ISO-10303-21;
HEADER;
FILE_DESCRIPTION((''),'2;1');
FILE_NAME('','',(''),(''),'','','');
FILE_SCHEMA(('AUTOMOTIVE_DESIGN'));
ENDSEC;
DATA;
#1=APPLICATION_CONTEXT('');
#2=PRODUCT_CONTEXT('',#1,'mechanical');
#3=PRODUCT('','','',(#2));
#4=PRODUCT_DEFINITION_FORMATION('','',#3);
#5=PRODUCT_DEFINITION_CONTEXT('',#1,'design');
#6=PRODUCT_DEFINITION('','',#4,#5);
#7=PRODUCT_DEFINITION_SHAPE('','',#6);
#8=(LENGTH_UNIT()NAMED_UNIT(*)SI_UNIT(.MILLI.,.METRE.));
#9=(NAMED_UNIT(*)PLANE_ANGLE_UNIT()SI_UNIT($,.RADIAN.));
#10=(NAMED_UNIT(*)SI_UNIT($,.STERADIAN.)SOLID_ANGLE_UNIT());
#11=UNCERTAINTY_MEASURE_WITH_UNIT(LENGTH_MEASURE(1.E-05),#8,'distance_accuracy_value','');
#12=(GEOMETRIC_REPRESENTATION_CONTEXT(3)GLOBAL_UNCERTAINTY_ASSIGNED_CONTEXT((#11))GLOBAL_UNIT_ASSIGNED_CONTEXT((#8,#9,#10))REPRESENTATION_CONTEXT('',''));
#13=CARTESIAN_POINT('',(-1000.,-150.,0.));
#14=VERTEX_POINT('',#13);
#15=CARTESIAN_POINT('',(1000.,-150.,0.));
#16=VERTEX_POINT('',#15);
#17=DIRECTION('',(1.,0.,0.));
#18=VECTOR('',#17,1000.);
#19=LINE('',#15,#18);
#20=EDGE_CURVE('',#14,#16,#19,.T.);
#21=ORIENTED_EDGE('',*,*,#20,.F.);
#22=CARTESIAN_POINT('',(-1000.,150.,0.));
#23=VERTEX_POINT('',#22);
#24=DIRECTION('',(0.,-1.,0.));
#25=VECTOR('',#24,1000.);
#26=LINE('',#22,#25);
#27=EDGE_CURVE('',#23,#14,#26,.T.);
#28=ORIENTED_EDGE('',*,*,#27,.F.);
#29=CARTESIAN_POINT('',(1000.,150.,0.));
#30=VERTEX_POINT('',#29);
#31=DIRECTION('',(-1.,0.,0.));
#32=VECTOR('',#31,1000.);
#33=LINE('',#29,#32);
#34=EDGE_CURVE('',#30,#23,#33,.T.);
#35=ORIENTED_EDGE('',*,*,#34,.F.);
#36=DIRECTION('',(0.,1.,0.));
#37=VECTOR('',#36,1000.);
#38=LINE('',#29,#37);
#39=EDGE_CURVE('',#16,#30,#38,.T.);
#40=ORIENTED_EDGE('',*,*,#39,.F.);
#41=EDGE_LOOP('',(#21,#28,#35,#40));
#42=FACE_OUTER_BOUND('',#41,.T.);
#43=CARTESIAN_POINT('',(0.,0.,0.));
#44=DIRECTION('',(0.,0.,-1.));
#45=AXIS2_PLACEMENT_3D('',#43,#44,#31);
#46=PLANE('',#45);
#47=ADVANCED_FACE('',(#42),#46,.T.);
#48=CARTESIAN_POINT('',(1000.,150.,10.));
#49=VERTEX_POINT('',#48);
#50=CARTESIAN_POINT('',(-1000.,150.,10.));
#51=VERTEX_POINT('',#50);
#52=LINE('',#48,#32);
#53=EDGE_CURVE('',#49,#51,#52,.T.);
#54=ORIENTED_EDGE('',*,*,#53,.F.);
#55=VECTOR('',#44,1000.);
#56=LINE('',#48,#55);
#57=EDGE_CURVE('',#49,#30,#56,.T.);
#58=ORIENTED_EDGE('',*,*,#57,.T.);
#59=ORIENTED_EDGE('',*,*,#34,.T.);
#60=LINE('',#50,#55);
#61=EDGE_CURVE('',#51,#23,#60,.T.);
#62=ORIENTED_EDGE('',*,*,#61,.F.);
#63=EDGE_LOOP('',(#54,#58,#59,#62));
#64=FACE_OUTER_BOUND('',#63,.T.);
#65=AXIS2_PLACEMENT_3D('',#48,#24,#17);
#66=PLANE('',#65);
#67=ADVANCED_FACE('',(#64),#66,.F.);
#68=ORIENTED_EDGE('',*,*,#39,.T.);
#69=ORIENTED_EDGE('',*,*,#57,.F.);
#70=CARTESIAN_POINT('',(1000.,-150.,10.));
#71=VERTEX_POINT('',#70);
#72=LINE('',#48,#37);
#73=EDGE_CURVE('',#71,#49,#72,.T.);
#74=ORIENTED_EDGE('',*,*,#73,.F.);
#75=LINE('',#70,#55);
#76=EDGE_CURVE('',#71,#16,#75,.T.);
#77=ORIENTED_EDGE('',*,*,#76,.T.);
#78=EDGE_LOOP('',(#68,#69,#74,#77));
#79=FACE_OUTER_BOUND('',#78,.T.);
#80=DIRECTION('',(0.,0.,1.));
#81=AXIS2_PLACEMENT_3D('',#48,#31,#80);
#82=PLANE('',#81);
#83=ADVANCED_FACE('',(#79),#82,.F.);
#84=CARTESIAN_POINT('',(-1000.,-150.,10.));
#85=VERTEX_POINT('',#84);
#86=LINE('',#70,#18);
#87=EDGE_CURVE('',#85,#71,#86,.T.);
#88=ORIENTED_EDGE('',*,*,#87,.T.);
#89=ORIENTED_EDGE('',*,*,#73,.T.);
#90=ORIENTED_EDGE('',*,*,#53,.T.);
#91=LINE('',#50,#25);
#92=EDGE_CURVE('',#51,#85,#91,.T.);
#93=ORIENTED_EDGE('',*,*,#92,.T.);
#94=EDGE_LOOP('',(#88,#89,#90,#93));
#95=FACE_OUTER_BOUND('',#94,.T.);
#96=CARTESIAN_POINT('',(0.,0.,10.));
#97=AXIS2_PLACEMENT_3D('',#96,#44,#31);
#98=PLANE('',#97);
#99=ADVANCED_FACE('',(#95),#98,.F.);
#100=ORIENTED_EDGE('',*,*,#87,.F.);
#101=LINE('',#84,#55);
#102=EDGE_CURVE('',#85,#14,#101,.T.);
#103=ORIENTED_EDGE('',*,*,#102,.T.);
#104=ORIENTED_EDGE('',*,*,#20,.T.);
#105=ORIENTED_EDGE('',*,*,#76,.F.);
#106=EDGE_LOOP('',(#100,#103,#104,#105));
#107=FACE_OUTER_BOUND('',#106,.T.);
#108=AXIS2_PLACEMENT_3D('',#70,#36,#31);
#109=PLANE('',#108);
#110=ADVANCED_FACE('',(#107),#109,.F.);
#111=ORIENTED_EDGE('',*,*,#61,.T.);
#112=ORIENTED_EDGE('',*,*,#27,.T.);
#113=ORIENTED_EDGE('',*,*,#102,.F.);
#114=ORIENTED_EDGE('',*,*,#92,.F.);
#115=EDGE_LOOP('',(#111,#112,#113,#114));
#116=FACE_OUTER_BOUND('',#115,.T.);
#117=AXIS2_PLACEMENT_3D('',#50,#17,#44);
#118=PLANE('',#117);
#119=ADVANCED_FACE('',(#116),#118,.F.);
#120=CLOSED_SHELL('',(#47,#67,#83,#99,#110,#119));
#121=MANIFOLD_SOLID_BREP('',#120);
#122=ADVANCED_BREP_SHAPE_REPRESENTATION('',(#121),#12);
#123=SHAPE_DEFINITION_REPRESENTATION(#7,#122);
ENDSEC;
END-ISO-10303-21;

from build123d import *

# Parameters (mm, degrees)
SKETCH1_W           = 2000
SKETCH1_H           = 300
BOSS_EXTRUDE1_DEPTH = 10


with BuildPart() as part:
    # Sketch1 → Boss-Extrude1 (new body)
    with BuildSketch(Plane.XY):
        Rectangle(SKETCH1_W, SKETCH1_H)
    extrude(amount=BOSS_EXTRUDE1_DEPTH)


solid = part.part
